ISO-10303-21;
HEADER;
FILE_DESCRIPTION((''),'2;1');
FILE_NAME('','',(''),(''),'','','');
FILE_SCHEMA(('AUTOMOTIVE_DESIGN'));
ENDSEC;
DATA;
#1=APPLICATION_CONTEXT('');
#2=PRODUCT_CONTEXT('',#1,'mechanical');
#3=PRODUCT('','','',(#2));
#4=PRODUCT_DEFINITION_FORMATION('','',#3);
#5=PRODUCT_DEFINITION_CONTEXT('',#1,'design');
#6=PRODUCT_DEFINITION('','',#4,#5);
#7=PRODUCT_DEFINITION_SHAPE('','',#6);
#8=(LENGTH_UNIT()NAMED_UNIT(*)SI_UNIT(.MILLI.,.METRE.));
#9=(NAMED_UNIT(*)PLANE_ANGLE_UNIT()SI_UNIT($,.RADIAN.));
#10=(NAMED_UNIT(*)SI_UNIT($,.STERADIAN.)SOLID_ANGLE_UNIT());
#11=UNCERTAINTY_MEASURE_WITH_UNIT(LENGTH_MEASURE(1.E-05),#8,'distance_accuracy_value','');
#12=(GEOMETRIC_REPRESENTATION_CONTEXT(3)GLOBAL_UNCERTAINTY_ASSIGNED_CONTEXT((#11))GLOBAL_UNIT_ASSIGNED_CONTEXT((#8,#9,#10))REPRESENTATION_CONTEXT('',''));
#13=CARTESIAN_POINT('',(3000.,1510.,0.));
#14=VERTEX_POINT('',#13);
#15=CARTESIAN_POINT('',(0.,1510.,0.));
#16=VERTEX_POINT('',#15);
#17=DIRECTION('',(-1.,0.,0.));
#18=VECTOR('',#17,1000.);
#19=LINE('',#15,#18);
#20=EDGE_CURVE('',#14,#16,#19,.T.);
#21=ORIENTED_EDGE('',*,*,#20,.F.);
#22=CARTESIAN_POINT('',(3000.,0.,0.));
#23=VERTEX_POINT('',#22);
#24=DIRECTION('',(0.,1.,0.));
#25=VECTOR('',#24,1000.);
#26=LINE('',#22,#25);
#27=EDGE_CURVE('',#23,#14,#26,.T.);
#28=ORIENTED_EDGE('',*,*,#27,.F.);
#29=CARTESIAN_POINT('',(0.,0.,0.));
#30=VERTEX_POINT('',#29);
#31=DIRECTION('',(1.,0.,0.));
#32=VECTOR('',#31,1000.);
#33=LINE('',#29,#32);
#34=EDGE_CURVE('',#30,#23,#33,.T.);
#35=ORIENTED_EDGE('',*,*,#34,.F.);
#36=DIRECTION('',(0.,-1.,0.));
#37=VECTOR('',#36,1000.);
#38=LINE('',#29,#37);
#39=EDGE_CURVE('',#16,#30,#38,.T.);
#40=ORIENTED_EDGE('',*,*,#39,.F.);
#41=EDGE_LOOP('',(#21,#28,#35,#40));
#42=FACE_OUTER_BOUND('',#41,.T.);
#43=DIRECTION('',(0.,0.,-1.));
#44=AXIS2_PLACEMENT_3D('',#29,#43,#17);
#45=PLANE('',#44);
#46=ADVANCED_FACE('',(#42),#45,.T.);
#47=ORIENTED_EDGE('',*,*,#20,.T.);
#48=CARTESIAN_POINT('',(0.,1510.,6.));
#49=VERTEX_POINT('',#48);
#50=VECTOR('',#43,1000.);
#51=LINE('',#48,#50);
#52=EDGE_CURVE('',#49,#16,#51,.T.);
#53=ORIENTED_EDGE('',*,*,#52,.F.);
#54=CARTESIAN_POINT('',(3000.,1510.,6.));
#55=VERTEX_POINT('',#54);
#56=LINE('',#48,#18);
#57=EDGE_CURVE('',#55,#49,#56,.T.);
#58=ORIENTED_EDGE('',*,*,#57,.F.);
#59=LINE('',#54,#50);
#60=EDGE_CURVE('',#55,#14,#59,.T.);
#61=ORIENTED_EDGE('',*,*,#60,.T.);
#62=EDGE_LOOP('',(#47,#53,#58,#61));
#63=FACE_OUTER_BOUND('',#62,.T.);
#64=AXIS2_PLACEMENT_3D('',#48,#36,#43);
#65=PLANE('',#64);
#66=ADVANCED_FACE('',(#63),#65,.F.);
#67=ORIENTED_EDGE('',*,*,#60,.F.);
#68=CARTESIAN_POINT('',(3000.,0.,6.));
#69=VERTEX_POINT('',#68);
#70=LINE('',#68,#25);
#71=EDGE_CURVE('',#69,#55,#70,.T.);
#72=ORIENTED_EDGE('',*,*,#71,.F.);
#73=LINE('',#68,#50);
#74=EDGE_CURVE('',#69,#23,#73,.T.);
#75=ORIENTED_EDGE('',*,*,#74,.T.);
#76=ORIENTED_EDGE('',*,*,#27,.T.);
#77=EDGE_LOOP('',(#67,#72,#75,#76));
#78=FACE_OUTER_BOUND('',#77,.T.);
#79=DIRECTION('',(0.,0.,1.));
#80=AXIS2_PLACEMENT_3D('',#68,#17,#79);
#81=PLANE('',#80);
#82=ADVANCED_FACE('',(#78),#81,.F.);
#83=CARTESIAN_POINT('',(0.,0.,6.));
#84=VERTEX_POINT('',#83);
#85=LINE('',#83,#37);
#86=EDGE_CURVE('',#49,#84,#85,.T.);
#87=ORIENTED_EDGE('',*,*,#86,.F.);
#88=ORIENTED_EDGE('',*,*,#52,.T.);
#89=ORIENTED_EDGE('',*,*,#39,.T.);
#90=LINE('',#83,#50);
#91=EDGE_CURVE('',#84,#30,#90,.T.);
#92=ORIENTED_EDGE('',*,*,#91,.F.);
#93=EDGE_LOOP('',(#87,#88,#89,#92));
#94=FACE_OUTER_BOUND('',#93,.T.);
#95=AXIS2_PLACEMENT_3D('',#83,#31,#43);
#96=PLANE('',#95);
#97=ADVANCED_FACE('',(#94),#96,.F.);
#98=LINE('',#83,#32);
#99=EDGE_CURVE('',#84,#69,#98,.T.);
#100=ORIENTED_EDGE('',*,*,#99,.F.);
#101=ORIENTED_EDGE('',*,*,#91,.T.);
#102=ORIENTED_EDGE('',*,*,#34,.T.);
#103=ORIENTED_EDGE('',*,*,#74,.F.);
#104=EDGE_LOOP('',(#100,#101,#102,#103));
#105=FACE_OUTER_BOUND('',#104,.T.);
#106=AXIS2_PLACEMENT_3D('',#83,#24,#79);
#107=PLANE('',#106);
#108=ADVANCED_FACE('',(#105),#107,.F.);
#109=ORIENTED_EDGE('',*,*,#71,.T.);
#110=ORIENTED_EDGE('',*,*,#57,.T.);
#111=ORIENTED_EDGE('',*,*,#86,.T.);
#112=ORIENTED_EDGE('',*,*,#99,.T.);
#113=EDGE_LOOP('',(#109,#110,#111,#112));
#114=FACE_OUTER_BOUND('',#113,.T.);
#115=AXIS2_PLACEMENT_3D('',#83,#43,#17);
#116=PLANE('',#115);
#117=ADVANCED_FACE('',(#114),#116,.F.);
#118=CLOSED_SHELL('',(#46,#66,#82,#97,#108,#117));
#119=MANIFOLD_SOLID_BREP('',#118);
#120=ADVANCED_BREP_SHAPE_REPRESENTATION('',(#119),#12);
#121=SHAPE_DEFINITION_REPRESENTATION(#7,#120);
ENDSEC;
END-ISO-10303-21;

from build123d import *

# Parameters (mm, degrees)
SKETCH1_W           = 3000
SKETCH1_H           = 1510
BOSS_EXTRUDE1_DEPTH = 6


with BuildPart() as part:
    # Sketch1 → Boss-Extrude1 (new body)
    with BuildSketch(Plane.XY):
        with Locations((1500, 755)):
            Rectangle(SKETCH1_W, SKETCH1_H)
    extrude(amount=BOSS_EXTRUDE1_DEPTH)


solid = part.part
